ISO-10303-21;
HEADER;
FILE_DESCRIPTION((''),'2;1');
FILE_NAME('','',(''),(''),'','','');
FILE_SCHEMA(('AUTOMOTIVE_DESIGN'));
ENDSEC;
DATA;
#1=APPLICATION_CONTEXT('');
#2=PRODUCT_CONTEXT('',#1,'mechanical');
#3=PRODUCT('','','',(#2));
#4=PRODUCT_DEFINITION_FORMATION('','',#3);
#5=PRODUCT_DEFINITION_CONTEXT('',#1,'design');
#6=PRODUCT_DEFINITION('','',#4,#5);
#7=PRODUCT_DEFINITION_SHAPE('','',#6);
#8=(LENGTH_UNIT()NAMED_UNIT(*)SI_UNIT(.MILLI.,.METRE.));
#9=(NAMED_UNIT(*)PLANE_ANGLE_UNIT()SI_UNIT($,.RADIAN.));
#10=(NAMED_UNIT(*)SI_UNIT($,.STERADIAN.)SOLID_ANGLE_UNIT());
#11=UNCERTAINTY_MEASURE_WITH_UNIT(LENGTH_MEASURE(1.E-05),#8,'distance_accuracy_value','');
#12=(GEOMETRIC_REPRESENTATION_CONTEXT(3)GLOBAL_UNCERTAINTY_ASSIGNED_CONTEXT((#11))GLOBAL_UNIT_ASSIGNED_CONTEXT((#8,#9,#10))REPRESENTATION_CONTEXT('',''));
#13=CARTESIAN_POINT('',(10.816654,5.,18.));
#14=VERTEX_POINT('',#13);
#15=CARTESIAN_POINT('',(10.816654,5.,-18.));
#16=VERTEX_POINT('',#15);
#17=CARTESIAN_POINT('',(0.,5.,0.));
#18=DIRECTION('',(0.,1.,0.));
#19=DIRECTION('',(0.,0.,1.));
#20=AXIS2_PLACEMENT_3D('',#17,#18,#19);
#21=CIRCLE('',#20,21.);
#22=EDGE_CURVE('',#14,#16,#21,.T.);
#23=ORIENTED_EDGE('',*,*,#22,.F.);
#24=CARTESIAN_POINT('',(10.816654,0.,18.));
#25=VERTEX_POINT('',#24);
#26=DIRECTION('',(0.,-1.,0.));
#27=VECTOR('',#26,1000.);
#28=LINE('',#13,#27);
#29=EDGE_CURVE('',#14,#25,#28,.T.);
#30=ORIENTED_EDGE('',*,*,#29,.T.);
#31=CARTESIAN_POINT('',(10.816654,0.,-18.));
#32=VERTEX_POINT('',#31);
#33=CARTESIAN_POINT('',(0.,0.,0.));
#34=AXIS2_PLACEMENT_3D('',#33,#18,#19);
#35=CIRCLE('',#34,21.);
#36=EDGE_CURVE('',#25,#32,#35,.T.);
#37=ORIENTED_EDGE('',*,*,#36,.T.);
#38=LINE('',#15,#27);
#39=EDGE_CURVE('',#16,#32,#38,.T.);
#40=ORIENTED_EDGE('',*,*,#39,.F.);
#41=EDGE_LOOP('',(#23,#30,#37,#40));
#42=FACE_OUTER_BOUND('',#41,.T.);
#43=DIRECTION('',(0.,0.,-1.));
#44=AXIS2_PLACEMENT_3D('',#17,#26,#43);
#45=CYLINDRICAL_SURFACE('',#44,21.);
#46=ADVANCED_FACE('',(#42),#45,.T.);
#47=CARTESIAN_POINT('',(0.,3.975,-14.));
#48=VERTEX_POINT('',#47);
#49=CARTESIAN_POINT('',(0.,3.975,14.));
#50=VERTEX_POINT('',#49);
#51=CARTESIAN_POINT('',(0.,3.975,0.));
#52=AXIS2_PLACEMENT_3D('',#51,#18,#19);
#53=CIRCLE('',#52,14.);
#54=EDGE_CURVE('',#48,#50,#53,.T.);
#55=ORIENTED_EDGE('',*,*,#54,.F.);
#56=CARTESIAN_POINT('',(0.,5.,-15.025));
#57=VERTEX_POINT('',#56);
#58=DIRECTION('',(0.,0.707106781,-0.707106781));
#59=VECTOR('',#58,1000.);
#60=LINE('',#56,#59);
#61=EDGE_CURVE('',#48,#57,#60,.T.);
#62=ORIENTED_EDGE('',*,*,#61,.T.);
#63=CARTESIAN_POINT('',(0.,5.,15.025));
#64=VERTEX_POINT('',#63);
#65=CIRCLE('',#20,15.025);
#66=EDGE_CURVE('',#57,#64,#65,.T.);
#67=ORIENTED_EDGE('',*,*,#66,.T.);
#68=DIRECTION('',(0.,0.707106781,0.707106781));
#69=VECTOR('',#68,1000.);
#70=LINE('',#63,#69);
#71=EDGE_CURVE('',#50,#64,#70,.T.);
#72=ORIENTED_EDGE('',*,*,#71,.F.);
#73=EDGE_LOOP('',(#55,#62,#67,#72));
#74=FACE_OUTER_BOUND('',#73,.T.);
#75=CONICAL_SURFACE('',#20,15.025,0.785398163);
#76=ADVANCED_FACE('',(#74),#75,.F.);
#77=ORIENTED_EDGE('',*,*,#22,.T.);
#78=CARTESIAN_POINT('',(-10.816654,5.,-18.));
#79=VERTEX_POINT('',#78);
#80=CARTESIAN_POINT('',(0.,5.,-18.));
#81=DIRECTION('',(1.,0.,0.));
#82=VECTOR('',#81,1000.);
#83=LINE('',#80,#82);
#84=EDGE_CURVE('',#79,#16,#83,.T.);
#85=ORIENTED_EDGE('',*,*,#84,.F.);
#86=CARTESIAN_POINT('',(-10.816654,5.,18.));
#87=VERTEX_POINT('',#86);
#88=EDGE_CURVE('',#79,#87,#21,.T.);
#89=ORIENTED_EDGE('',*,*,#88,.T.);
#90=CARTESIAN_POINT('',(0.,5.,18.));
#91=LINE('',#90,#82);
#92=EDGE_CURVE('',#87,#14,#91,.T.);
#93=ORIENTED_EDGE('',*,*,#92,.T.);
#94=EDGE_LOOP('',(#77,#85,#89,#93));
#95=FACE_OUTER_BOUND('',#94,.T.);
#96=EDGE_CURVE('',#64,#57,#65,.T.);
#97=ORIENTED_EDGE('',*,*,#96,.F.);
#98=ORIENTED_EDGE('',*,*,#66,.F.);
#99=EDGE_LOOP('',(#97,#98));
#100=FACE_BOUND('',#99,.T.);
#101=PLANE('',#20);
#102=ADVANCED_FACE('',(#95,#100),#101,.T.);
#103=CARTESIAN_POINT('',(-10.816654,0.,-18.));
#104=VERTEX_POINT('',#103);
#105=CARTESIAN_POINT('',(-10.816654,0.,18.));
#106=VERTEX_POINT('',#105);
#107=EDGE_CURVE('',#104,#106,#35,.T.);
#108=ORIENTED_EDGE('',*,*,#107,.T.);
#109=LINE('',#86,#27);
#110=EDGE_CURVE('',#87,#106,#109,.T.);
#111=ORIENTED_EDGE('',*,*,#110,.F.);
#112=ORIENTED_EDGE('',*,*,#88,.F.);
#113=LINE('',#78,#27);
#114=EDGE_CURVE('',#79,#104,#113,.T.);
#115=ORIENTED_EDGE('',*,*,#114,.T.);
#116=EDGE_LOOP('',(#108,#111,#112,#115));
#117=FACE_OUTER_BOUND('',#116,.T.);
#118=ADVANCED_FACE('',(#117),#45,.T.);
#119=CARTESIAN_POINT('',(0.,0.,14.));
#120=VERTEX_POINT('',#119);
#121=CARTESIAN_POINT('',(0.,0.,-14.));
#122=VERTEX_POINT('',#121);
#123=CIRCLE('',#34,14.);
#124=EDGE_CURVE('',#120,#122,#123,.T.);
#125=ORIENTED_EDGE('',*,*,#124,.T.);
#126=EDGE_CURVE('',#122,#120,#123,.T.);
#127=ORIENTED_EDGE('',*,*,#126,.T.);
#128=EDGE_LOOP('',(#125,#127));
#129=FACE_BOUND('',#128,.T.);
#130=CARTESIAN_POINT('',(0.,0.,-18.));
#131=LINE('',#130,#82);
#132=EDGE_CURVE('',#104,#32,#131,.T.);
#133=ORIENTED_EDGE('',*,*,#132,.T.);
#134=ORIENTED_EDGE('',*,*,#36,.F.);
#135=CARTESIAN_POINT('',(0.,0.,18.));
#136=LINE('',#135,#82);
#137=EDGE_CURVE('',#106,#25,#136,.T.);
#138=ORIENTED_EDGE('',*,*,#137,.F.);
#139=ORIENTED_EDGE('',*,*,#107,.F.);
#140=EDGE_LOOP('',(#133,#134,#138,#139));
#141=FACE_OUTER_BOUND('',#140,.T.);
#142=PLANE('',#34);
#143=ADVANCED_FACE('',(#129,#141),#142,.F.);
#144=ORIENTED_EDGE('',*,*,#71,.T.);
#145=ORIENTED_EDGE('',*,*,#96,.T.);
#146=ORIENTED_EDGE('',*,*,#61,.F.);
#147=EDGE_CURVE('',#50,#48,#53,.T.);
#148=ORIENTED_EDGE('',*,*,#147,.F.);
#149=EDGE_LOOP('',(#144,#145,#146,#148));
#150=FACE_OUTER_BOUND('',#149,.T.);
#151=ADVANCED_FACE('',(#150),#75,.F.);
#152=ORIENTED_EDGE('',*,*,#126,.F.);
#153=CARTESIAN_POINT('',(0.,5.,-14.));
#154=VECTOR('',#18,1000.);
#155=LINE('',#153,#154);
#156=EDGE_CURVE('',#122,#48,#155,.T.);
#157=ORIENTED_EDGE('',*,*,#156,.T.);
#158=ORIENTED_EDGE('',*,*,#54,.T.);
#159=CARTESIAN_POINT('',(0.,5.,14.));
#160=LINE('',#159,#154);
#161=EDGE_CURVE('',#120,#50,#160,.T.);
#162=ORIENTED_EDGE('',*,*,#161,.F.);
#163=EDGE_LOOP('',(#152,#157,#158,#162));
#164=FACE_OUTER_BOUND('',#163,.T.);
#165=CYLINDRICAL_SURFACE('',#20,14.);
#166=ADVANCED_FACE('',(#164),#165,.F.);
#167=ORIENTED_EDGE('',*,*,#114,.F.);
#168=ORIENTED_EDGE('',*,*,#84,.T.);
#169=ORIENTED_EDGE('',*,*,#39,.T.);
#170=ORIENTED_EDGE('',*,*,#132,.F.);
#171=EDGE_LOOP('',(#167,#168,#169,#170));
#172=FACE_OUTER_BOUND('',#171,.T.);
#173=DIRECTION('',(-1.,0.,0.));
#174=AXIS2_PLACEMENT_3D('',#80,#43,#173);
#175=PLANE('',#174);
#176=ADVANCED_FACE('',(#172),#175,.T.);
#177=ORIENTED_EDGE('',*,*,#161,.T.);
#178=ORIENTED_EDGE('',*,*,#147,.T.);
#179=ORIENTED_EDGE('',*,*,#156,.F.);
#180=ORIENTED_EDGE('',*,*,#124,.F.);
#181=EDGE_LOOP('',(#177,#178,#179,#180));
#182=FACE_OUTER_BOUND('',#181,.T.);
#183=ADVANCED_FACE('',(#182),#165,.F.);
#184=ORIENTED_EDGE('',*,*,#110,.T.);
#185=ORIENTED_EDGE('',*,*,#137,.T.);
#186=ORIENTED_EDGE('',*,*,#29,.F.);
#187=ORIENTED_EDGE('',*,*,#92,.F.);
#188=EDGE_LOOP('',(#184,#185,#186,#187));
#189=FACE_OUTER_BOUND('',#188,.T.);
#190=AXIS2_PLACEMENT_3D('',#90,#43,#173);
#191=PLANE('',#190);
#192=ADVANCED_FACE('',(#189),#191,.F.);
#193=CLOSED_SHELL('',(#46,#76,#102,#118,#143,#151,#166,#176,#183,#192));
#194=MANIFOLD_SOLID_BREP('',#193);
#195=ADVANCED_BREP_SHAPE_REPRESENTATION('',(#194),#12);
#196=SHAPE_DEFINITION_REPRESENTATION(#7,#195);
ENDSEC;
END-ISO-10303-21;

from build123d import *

# Parameters (mm, degrees)
BOSS_EXTRUDE1_DEPTH              = 5
M30X2_0_TAPPED_HOLE1_D           = 28
M30X2_0_TAPPED_HOLE1_DEPTH       = 70
M30X2_0_TAPPED_HOLE1_CSINK_D     = 30.05
M30X2_0_TAPPED_HOLE1_CSINK_ANGLE = 90
M30X2_0_TAPPED_HOLE1_TIP         = 8.412048666


with BuildPart() as part:
    # Sketch1 → Boss-Extrude1 (new body)
    with BuildSketch(Plane(origin=(0, 0, 0), x_dir=(1, 0, 0), z_dir=(0, 1, 0))):
        with BuildLine():
            Line((10.816653826, 18), (-10.816653826, 18))
            ThreePointArc((-10.816653826, 18), (-21, 0), (-10.816653826, -18))
            Line((-10.816653826, -18), (10.816653826, -18))
            ThreePointArc((10.816653826, -18), (18.277714988, -10.340461055), (21, 0))
            ThreePointArc((21, 0), (18.277714988, 10.340461055), (10.816653826, 18))
        make_face()
    extrude(amount=BOSS_EXTRUDE1_DEPTH)

    # M30x2.0 Tapped Hole1
    with Locations(Plane(origin=(0, 5, 0), x_dir=(1, 0, 0), z_dir=(0, 1, 0))):
        with Locations((0, 0)):
            CounterSinkHole(M30X2_0_TAPPED_HOLE1_D / 2, M30X2_0_TAPPED_HOLE1_CSINK_D / 2, depth=M30X2_0_TAPPED_HOLE1_DEPTH, counter_sink_angle=M30X2_0_TAPPED_HOLE1_CSINK_ANGLE)
            with Locations((0, 0, -(M30X2_0_TAPPED_HOLE1_DEPTH + M30X2_0_TAPPED_HOLE1_TIP / 2))):  # 118° drill point
                Cone(0, M30X2_0_TAPPED_HOLE1_D / 2, M30X2_0_TAPPED_HOLE1_TIP, mode=Mode.SUBTRACT)


solid = part.part
